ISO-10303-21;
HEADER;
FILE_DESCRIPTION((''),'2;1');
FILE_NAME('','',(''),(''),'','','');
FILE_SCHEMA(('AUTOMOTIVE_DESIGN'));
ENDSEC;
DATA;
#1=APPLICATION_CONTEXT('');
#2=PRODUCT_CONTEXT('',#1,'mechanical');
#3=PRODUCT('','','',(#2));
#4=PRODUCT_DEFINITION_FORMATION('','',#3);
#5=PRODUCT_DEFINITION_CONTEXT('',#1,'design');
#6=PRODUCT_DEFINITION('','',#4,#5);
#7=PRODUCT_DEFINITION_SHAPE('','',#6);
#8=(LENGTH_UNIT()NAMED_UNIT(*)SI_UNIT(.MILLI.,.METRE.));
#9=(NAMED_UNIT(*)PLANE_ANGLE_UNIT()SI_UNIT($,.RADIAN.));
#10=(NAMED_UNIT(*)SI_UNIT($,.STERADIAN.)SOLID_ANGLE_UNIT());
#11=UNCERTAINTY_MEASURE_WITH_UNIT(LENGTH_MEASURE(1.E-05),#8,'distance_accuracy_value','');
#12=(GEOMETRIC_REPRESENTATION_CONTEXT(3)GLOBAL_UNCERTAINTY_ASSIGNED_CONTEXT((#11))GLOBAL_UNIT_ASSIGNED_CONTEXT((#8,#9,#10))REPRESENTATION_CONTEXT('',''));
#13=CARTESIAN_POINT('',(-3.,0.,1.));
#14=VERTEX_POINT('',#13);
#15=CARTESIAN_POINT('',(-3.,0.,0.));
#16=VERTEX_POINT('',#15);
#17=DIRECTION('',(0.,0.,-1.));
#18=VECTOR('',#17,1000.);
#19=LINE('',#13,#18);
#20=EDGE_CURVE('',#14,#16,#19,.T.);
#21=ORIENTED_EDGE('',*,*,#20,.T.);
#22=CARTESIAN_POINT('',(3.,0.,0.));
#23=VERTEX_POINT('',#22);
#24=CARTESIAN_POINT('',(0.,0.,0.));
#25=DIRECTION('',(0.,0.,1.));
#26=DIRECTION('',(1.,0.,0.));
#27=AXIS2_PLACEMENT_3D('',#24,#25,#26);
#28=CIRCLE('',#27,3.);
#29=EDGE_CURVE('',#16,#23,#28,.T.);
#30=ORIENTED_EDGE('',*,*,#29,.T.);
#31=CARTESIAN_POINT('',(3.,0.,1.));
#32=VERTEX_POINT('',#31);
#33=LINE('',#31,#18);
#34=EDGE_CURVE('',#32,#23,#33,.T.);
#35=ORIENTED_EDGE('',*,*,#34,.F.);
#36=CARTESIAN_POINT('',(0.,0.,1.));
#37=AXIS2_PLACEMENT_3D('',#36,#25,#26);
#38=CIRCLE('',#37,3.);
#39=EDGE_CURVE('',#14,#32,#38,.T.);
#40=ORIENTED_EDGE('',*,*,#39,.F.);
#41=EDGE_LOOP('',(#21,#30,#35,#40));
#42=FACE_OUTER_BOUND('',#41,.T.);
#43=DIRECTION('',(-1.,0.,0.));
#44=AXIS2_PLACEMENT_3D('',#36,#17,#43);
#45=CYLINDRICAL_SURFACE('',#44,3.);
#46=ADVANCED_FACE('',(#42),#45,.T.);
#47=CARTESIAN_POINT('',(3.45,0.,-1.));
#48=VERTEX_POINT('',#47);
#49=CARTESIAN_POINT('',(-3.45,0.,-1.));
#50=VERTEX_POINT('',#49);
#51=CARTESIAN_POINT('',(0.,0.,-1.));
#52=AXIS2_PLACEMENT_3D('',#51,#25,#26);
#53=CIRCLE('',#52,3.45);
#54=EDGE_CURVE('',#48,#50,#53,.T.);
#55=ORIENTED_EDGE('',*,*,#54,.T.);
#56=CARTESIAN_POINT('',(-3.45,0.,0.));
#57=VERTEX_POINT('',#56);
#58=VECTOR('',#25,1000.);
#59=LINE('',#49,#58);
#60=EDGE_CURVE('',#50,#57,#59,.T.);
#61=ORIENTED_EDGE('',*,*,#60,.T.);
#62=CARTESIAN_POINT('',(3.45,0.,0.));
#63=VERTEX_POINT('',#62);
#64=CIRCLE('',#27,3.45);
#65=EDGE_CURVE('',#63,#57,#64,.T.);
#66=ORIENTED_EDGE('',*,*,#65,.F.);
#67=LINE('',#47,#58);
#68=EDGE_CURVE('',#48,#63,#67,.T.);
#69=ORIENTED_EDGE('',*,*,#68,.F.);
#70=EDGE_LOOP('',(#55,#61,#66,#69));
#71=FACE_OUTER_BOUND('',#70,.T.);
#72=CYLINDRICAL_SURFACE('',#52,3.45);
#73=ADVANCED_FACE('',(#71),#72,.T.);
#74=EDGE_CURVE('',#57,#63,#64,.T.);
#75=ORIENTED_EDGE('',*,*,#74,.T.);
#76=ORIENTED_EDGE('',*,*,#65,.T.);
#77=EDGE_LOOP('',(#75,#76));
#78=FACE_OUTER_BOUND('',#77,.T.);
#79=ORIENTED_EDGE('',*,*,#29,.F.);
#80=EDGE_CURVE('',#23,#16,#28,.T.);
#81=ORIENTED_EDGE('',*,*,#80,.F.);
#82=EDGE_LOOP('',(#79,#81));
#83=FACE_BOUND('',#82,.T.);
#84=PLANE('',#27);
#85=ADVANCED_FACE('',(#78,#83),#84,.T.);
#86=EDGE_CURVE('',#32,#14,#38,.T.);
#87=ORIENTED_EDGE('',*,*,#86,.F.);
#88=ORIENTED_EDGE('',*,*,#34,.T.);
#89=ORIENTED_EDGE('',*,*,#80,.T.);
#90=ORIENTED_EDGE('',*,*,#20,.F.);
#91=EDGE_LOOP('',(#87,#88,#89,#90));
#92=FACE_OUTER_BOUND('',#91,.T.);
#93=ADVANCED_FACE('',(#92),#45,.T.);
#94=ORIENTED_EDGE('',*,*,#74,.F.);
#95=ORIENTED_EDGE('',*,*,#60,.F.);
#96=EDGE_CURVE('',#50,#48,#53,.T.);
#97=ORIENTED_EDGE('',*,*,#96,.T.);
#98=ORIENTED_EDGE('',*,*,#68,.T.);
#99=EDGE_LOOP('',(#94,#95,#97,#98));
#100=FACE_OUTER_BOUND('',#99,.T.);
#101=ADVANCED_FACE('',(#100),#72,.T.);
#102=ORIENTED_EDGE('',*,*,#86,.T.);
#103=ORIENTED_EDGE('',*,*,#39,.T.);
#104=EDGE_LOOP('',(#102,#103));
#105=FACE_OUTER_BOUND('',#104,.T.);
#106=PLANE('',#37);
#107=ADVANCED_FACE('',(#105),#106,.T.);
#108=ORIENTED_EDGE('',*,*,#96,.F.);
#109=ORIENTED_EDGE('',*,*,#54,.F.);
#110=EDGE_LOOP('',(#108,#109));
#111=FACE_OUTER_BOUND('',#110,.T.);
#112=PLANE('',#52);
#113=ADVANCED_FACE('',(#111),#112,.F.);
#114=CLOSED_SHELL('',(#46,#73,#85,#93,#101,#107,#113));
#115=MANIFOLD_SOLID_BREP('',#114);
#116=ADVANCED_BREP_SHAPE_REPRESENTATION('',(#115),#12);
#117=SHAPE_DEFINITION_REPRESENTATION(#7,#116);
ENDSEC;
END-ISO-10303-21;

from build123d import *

# Parameters (mm, degrees)
SKETCH_1_3_R        = 3
BOSS_EXTRUDE1_DEPTH = 1
SKETCH_1_3_2_R      = 3.45
BOSS_EXTRUDE2_DEPTH = 1


with BuildPart() as part:
    # Sketch 1_3 → Boss-Extrude1 (new body)
    with BuildSketch(Plane.XY):
        Circle(SKETCH_1_3_R)
    extrude(amount=BOSS_EXTRUDE1_DEPTH)

    # Sketch 1_3 2 → Boss-Extrude2 (add)
    with BuildSketch(Plane.XY):
        Circle(SKETCH_1_3_2_R)
    extrude(amount=-BOSS_EXTRUDE2_DEPTH)


solid = part.part
